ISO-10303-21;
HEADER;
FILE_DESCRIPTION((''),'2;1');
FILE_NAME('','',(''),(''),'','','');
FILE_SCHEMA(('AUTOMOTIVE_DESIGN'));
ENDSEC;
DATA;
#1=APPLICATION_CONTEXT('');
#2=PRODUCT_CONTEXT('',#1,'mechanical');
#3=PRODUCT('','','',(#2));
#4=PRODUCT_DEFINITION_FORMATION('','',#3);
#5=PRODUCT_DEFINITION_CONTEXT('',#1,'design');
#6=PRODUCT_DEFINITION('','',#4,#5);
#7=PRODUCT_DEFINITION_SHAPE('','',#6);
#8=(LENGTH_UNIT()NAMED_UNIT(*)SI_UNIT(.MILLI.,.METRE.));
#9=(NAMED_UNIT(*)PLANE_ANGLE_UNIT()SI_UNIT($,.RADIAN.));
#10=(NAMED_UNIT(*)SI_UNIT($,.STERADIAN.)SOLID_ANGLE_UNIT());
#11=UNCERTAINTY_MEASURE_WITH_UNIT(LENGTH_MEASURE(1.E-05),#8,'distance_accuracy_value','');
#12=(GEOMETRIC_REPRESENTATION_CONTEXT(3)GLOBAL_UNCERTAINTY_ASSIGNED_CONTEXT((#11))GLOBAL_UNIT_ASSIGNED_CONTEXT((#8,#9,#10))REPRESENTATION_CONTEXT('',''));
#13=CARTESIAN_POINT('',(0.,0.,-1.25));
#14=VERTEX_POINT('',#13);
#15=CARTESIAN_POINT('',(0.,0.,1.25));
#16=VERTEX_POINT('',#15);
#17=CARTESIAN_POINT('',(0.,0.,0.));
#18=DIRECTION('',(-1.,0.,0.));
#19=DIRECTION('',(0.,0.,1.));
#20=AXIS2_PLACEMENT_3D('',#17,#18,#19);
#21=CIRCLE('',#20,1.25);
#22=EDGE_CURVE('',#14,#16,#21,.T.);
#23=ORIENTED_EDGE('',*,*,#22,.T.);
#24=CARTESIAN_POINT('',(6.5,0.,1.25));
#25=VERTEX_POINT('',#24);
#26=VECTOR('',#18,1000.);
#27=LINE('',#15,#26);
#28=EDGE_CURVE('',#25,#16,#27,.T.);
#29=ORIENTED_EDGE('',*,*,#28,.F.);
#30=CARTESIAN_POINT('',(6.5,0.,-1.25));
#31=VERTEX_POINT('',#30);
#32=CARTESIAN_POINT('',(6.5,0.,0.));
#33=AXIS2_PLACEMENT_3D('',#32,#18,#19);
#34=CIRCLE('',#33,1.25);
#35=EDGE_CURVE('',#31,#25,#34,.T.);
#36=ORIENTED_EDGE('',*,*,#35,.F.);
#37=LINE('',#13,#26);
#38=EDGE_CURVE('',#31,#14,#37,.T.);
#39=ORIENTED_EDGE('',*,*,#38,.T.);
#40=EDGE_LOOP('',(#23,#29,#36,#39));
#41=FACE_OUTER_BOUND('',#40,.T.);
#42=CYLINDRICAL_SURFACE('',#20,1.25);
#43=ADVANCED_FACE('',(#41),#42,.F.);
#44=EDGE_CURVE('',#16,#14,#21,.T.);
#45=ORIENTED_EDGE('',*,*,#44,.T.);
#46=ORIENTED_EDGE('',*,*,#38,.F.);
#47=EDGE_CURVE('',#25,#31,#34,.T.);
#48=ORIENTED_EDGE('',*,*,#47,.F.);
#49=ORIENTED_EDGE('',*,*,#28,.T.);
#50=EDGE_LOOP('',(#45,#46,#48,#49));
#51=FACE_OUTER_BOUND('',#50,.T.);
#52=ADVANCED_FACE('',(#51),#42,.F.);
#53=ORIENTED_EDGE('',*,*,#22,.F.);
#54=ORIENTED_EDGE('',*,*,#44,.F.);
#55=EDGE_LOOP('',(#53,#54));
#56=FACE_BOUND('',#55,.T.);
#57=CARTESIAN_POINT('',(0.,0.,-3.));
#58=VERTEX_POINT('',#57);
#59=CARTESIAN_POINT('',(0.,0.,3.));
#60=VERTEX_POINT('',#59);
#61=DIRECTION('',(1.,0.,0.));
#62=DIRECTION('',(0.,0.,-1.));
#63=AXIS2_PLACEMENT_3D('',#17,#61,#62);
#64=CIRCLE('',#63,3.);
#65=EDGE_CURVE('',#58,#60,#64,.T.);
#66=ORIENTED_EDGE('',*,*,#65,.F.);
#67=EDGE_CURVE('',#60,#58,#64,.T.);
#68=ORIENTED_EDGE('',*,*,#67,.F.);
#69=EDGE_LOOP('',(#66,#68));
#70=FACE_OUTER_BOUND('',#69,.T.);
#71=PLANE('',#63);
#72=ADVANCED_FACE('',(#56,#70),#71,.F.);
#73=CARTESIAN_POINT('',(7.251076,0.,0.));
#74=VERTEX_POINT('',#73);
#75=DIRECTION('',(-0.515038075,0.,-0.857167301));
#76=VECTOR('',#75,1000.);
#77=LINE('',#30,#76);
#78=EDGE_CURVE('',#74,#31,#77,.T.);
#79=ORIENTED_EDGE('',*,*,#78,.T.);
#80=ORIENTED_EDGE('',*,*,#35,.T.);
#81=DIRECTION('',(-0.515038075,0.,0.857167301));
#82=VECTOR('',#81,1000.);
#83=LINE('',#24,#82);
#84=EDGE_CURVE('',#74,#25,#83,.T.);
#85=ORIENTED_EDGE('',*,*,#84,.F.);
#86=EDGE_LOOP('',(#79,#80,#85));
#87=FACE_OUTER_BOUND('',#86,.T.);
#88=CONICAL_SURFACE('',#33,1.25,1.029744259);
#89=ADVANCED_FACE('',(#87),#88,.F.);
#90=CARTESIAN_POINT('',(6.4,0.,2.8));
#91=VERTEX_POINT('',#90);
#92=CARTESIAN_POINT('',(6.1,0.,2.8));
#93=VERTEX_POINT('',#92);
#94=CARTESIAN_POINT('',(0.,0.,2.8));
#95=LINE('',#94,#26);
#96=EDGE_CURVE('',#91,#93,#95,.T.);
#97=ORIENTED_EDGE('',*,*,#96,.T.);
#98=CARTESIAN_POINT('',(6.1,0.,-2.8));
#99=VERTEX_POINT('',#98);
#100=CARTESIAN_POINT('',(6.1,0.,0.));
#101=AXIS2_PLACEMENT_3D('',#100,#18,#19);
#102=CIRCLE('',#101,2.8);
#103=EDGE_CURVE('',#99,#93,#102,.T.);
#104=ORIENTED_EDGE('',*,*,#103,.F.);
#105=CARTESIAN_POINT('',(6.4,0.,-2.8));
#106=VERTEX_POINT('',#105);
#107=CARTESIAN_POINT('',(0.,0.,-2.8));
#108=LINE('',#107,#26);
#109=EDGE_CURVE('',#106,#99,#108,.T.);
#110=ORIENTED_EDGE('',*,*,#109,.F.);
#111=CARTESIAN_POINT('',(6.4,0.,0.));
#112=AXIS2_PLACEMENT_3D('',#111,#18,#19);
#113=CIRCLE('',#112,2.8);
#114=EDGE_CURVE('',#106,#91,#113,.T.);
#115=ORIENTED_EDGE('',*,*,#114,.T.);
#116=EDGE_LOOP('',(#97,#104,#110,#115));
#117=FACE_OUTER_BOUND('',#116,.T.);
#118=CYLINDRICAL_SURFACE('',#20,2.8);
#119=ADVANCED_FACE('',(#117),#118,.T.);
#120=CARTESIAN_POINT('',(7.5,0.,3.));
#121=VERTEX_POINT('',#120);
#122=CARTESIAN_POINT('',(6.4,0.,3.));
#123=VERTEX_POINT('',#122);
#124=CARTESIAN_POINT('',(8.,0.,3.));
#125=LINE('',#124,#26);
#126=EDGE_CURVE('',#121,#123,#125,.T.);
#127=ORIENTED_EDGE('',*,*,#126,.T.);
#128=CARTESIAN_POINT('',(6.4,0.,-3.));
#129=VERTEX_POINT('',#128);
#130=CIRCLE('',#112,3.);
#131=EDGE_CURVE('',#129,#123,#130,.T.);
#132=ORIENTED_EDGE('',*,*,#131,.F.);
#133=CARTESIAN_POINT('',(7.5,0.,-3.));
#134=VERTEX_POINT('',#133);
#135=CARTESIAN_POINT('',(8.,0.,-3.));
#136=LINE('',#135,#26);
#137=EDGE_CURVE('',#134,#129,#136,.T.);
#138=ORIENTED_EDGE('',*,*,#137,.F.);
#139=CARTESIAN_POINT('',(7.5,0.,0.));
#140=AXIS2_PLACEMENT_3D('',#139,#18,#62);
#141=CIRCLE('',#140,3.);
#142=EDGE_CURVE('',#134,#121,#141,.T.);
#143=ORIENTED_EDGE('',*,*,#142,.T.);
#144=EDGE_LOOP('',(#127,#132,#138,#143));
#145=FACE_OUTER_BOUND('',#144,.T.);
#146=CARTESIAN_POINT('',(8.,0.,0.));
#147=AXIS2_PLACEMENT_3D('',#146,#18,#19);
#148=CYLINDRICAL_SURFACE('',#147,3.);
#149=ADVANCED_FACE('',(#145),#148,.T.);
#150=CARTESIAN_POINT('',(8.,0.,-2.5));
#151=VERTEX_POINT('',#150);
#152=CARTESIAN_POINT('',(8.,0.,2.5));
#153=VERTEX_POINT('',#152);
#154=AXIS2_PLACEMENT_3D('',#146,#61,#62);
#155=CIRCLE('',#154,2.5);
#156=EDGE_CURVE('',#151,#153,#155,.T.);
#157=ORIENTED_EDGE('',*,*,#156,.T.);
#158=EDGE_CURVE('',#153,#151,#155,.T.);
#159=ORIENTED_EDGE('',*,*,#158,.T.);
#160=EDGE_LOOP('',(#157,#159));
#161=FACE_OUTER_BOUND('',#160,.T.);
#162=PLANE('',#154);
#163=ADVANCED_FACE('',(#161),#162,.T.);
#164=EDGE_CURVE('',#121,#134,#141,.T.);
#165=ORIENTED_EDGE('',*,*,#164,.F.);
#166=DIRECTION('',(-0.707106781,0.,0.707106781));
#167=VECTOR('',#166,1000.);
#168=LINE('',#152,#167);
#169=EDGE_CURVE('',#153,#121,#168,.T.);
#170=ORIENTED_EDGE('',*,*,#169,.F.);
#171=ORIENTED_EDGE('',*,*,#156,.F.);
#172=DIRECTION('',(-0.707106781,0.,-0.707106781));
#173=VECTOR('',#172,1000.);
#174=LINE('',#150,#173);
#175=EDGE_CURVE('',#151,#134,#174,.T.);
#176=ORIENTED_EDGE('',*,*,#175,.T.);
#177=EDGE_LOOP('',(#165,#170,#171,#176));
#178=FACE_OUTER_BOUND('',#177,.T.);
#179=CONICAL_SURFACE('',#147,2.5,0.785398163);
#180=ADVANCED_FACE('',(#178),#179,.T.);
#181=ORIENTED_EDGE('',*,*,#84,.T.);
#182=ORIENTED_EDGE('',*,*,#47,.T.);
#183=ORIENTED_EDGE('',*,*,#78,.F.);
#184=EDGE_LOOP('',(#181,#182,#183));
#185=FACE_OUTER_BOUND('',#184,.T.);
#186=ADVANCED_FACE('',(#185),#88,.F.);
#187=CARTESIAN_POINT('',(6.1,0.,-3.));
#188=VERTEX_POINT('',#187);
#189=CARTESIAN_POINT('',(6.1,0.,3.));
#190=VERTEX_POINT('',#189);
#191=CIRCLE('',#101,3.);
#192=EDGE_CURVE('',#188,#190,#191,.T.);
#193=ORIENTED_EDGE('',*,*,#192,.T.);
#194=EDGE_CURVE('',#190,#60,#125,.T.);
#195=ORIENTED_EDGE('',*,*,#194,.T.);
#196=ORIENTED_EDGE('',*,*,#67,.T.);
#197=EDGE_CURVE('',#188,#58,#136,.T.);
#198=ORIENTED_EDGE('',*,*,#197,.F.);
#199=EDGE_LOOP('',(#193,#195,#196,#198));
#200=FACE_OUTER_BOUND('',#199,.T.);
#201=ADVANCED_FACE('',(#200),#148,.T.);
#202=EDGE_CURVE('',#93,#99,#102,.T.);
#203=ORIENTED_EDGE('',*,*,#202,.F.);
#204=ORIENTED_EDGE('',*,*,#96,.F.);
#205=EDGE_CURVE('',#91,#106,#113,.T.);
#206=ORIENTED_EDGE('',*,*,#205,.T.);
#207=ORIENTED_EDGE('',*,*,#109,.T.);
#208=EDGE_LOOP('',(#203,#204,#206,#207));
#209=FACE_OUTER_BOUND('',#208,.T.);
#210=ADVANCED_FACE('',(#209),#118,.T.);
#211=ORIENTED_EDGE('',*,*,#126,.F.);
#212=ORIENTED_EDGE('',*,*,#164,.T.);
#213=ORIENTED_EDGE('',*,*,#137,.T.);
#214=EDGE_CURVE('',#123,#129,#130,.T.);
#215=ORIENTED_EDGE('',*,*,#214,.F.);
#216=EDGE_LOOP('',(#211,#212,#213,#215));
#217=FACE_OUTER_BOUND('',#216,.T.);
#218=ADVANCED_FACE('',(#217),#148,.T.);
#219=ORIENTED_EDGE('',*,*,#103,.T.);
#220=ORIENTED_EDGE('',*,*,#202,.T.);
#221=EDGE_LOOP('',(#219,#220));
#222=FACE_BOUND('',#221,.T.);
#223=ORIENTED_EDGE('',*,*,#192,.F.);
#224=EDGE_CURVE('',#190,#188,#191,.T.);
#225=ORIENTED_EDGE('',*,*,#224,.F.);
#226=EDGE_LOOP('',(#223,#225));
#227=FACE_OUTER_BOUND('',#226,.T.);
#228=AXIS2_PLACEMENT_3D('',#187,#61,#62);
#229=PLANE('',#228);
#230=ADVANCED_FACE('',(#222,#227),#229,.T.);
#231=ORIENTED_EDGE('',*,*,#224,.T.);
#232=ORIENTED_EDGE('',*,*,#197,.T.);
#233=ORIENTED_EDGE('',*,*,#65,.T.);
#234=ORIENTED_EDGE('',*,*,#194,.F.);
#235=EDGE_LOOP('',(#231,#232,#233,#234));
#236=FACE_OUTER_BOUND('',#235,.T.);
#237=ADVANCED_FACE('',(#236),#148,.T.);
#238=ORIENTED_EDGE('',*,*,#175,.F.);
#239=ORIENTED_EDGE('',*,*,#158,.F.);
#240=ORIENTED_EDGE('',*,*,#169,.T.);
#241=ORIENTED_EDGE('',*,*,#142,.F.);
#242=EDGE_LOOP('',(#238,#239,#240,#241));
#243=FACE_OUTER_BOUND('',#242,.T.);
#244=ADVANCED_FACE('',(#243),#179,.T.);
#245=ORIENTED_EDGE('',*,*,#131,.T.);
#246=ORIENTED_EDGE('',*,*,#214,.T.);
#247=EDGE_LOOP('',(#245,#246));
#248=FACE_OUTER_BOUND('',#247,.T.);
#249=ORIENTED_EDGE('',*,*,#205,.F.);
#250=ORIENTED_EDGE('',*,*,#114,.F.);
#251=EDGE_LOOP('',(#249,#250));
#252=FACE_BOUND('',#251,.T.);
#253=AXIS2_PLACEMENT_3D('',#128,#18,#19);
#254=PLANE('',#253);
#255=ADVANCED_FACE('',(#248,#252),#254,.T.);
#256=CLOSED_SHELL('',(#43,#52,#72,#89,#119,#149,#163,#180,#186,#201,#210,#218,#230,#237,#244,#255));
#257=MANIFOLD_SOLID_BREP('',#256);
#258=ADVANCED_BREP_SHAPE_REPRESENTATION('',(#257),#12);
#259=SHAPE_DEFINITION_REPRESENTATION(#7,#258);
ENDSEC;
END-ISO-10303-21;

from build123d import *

# Parameters (mm, degrees)
SKETCH1_R             = 3
BOSS_EXTRUDE1_DEPTH   = 8
CHAMFER1_SIZE         = 0.5
M3_TAPPED_HOLE1_D     = 2.5
M3_TAPPED_HOLE1_DEPTH = 6.5
M3_TAPPED_HOLE1_TIP   = 0.751075774
SKETCH3_W             = 0.3
SKETCH3_H             = 0.2


with BuildPart() as part:
    # Sketch1 → Boss-Extrude1 (new body)
    with BuildSketch(Plane(origin=(0, 0, 0), x_dir=(0, 0, -1), z_dir=(1, 0, 0))):
        Circle(SKETCH1_R)
    extrude(amount=BOSS_EXTRUDE1_DEPTH)

    # Chamfer1
    chamfer1_edges = [part.edges().sort_by_distance(p)[0] for p in [
        (8, 0, 3),
    ]]
    chamfer(chamfer1_edges, length=CHAMFER1_SIZE)

    # M3 Tapped Hole1
    with Locations(Plane(origin=(0, 0, 0), x_dir=(0, 0, -1), z_dir=(-1, 0, 0))):
        with Locations((0, 0)):
            Hole(M3_TAPPED_HOLE1_D / 2, depth=M3_TAPPED_HOLE1_DEPTH)
            with Locations((0, 0, -(M3_TAPPED_HOLE1_DEPTH + M3_TAPPED_HOLE1_TIP / 2))):  # 118° drill point
                Cone(0, M3_TAPPED_HOLE1_D / 2, M3_TAPPED_HOLE1_TIP, mode=Mode.SUBTRACT)

    # Sketch3 → Cut-Revolve1 (revolve, cut)
    with BuildSketch(Plane(origin=(0, 0, 0), x_dir=(1, 0, 0), z_dir=(0, 1, 0)), mode=Mode.PRIVATE) as cut_revolve1_sk:
        with Locations((6.25, 2.9)):
            Rectangle(SKETCH3_W, SKETCH3_H)
    revolve(cut_revolve1_sk.sketch.rotate(Axis((0, 0, 0), (1, 0, 0)), 180), axis=Axis((0, 0, 0), (1, 0, 0)), mode=Mode.SUBTRACT)


solid = part.part
